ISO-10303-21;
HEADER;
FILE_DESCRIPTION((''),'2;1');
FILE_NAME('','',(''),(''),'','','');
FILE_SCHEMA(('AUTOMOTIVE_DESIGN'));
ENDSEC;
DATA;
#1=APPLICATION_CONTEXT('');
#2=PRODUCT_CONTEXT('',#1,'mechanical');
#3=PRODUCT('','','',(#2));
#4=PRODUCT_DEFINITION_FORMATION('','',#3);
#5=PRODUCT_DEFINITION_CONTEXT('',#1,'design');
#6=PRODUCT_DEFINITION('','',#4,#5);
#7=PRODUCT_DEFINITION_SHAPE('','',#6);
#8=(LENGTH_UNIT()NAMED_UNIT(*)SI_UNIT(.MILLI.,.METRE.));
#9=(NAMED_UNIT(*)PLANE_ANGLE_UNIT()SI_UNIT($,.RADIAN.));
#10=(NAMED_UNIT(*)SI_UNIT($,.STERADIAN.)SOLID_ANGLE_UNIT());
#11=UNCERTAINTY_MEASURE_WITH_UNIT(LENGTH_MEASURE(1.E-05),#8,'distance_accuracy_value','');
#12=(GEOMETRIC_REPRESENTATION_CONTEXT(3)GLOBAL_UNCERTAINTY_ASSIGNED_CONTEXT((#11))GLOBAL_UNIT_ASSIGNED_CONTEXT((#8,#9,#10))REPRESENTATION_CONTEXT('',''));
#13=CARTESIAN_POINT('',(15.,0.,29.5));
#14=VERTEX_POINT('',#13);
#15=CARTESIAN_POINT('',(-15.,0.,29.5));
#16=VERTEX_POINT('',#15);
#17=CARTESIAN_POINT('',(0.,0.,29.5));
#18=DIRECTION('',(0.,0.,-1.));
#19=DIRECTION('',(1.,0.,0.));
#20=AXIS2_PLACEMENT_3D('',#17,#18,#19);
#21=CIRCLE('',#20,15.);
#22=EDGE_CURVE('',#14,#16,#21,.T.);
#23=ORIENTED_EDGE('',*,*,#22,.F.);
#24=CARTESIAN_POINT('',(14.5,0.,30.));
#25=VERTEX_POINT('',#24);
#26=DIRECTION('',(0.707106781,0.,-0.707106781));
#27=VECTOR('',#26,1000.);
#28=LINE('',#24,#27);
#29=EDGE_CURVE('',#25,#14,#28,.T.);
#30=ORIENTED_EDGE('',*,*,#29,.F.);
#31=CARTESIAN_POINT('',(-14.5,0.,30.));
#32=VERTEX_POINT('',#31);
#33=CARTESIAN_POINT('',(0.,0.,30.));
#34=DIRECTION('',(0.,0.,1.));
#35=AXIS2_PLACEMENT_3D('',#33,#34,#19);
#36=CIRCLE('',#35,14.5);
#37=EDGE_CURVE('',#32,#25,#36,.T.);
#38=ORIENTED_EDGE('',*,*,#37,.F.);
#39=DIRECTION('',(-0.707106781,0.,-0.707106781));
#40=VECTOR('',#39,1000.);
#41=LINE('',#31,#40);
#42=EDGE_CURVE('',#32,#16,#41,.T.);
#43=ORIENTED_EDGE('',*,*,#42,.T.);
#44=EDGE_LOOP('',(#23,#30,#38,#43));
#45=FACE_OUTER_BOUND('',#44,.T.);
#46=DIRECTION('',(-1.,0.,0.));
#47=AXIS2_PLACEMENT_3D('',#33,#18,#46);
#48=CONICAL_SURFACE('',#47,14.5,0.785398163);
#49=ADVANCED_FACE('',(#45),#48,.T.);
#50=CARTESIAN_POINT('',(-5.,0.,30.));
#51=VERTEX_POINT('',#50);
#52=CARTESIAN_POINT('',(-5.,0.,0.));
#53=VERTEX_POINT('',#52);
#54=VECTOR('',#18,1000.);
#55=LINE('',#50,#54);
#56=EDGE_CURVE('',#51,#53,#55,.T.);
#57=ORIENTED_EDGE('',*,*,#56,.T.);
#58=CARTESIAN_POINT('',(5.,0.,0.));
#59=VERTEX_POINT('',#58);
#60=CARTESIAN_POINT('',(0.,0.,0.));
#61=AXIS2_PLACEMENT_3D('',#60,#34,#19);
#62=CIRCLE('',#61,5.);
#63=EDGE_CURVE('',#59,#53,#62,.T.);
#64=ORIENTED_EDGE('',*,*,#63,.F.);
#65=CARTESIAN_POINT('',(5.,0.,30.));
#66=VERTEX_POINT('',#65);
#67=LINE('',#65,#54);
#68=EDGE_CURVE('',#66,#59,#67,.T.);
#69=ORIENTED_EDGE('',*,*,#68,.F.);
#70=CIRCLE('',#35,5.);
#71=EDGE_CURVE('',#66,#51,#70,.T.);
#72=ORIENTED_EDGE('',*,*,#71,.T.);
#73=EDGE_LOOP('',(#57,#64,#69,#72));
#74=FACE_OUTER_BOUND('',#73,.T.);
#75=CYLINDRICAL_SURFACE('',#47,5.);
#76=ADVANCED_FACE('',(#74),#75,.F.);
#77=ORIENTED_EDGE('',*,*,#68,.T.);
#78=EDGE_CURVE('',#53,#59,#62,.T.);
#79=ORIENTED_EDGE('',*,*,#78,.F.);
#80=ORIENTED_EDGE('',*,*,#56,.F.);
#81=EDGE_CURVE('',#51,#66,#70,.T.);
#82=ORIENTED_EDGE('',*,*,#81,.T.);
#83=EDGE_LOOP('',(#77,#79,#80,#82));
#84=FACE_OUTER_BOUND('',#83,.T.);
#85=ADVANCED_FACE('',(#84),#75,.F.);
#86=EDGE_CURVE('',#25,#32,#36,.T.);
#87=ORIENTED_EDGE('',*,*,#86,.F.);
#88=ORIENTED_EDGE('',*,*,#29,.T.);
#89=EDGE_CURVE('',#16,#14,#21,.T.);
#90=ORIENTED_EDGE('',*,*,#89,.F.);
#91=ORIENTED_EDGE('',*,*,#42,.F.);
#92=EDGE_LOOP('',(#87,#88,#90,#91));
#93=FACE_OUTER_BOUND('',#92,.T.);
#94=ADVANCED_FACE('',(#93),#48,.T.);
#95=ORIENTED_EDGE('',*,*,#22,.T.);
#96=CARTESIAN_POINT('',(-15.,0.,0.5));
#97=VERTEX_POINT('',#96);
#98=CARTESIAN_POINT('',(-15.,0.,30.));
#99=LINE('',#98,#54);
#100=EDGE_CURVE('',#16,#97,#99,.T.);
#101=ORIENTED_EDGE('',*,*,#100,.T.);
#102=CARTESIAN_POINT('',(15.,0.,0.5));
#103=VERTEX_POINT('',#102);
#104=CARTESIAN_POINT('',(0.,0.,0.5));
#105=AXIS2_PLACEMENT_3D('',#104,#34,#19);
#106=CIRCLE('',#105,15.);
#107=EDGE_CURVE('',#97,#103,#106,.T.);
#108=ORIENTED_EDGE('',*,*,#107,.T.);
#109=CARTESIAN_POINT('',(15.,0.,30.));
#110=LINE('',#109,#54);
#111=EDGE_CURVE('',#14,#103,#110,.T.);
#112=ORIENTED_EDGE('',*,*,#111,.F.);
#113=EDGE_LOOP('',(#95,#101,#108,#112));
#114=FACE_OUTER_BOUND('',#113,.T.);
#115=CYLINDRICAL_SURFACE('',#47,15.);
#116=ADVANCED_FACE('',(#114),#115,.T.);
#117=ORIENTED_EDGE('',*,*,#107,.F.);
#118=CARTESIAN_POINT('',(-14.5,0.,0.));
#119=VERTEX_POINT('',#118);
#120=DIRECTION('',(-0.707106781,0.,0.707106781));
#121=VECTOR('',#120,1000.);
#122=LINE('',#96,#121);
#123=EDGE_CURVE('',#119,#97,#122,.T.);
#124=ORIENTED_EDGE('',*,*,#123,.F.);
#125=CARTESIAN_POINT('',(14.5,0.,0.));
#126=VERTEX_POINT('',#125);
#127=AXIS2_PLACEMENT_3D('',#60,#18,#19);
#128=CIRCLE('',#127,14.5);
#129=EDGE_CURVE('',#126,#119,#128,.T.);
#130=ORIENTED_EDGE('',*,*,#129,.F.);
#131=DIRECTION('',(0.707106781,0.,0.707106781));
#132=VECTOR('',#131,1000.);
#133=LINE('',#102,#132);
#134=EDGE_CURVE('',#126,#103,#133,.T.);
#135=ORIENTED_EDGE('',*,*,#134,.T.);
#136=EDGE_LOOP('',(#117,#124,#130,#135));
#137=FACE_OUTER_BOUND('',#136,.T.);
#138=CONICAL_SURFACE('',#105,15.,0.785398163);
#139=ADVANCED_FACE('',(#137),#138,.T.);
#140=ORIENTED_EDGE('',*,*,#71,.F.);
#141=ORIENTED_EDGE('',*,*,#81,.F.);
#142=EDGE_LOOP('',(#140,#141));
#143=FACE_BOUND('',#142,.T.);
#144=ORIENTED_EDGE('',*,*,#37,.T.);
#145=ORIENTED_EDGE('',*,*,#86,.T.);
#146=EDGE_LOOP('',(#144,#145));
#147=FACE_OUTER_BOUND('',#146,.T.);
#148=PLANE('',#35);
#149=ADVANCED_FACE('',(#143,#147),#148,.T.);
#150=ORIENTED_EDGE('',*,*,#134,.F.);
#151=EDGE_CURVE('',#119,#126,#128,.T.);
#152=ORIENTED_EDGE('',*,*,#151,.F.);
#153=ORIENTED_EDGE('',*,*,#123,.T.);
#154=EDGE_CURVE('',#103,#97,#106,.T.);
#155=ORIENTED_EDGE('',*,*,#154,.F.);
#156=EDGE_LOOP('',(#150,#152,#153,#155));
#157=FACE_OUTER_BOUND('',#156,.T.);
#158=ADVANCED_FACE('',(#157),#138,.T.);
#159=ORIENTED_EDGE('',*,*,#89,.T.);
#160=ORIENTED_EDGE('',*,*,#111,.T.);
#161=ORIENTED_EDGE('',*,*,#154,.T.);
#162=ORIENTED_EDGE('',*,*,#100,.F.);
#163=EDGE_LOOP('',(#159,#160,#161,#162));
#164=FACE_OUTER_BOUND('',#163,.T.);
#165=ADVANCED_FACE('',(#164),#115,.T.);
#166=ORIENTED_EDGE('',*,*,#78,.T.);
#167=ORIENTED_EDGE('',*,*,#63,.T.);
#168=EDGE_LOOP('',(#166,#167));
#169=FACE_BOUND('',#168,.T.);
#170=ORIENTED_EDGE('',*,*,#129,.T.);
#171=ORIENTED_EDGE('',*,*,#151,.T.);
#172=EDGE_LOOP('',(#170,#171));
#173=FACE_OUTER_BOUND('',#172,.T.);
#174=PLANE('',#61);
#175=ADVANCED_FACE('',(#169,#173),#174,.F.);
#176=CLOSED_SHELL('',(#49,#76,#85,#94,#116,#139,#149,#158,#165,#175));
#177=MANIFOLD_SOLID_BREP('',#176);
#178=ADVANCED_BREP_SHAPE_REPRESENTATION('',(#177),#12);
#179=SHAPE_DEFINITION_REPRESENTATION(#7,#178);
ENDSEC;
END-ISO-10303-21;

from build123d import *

# Parameters (mm, degrees)
SKETCH1_R           = 15
SKETCH1_R_2         = 5
BOSS_EXTRUDE1_DEPTH = 30
CHAMFER1_SIZE       = 0.5


with BuildPart() as part:
    # Sketch1 → Boss-Extrude1 (new body)
    with BuildSketch(Plane.XY):
        Circle(SKETCH1_R)
        Circle(SKETCH1_R_2, mode=Mode.SUBTRACT)
    extrude(amount=BOSS_EXTRUDE1_DEPTH)

    # Chamfer1
    chamfer1_edges = [part.edges().sort_by_distance(p)[0] for p in [
        (-15, 0, 0),
        (-15, 0, 30),
    ]]
    chamfer(chamfer1_edges, length=CHAMFER1_SIZE)


solid = part.part
